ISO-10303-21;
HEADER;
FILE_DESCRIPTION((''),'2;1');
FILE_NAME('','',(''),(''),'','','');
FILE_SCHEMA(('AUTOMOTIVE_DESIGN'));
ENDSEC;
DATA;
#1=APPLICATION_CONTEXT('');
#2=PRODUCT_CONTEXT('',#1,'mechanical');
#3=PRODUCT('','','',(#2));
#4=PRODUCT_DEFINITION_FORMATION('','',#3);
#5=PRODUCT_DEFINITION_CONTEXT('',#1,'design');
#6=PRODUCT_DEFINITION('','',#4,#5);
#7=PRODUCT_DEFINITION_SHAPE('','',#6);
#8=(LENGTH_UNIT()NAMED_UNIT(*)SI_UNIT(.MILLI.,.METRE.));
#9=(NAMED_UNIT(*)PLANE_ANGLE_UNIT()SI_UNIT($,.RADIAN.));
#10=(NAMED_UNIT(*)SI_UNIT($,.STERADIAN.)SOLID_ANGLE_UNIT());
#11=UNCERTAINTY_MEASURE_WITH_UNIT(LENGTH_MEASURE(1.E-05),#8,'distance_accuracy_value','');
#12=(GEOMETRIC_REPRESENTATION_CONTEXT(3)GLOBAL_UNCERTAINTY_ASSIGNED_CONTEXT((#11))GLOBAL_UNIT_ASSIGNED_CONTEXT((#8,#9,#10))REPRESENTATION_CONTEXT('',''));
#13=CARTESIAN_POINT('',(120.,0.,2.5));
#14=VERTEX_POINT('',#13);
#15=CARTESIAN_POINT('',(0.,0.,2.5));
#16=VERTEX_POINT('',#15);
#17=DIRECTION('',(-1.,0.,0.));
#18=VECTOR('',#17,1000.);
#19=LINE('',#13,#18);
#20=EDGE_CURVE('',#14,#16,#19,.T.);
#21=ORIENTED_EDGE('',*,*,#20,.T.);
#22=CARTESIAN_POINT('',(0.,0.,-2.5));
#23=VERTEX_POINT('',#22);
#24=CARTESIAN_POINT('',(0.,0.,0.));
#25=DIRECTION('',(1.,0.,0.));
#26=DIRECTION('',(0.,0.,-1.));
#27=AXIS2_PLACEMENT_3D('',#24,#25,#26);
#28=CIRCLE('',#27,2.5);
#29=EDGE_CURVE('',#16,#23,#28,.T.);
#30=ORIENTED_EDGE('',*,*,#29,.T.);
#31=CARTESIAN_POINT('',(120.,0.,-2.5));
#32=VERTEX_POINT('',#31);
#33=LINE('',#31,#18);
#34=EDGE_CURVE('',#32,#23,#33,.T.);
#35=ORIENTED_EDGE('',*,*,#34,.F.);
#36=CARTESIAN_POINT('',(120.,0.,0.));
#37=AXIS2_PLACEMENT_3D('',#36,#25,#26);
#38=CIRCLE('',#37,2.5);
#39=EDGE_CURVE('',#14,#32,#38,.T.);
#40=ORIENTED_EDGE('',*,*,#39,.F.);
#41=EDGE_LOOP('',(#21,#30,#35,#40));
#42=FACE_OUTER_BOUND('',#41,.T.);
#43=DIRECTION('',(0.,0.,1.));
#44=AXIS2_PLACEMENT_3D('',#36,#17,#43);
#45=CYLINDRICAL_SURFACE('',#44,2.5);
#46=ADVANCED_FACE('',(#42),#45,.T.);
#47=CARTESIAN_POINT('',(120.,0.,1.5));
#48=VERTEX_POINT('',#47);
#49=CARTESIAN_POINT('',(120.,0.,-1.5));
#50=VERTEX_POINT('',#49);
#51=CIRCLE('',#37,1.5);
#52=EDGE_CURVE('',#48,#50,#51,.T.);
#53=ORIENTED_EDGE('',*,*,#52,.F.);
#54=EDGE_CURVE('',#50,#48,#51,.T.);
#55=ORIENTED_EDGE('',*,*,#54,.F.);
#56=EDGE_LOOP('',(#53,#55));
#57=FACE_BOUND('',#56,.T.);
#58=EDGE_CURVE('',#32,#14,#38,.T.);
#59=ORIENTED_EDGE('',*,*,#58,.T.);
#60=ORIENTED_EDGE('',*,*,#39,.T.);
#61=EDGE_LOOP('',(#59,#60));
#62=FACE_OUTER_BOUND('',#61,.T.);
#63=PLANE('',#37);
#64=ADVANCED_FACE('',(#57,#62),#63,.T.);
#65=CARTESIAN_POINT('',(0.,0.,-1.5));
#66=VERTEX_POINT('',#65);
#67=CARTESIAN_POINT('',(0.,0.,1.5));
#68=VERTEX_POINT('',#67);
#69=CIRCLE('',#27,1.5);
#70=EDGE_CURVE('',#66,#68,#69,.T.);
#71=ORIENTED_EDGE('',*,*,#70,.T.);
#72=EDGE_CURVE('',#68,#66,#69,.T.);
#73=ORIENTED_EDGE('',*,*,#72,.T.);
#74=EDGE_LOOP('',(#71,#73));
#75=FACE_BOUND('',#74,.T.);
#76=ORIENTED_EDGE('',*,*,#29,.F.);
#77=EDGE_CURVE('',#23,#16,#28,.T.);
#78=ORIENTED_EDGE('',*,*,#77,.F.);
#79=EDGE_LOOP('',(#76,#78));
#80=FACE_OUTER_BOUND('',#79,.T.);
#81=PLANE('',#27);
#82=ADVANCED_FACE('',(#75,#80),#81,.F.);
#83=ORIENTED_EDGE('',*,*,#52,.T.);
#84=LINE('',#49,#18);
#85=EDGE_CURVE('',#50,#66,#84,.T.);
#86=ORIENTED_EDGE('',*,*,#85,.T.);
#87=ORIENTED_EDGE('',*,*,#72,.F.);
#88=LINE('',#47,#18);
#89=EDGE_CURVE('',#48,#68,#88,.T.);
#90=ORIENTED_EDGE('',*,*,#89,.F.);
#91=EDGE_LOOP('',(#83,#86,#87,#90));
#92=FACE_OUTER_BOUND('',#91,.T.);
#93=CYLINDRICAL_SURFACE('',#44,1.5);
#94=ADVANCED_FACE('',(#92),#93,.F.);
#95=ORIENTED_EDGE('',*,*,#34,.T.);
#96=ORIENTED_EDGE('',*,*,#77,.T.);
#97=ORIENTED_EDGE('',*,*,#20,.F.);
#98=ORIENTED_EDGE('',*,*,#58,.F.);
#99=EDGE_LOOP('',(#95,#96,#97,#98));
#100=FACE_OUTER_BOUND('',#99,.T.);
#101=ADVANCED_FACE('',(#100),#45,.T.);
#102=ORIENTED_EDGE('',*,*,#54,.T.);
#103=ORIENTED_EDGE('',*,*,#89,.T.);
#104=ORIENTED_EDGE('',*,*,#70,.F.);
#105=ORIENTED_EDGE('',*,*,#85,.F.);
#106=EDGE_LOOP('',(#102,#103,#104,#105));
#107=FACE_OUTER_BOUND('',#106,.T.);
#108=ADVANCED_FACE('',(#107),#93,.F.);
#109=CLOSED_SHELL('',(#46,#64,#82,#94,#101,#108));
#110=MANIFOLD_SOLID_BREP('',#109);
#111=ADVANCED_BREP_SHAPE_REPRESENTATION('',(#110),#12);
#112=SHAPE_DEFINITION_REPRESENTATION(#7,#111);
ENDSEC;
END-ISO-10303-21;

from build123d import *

# Parameters (mm, degrees)
SKETCH_1_R      = 2.5
SKETCH_1_R_2    = 1.5
EXTRUDE_1_DEPTH = 120


with BuildPart() as part:
    # 草图1 → 凸台-拉伸1 (new body)
    with BuildSketch(Plane(origin=(0, 0, 0), x_dir=(0, 0, -1), z_dir=(1, 0, 0))):
        Circle(SKETCH_1_R)
        Circle(SKETCH_1_R_2, mode=Mode.SUBTRACT)
    extrude(amount=EXTRUDE_1_DEPTH)


solid = part.part
